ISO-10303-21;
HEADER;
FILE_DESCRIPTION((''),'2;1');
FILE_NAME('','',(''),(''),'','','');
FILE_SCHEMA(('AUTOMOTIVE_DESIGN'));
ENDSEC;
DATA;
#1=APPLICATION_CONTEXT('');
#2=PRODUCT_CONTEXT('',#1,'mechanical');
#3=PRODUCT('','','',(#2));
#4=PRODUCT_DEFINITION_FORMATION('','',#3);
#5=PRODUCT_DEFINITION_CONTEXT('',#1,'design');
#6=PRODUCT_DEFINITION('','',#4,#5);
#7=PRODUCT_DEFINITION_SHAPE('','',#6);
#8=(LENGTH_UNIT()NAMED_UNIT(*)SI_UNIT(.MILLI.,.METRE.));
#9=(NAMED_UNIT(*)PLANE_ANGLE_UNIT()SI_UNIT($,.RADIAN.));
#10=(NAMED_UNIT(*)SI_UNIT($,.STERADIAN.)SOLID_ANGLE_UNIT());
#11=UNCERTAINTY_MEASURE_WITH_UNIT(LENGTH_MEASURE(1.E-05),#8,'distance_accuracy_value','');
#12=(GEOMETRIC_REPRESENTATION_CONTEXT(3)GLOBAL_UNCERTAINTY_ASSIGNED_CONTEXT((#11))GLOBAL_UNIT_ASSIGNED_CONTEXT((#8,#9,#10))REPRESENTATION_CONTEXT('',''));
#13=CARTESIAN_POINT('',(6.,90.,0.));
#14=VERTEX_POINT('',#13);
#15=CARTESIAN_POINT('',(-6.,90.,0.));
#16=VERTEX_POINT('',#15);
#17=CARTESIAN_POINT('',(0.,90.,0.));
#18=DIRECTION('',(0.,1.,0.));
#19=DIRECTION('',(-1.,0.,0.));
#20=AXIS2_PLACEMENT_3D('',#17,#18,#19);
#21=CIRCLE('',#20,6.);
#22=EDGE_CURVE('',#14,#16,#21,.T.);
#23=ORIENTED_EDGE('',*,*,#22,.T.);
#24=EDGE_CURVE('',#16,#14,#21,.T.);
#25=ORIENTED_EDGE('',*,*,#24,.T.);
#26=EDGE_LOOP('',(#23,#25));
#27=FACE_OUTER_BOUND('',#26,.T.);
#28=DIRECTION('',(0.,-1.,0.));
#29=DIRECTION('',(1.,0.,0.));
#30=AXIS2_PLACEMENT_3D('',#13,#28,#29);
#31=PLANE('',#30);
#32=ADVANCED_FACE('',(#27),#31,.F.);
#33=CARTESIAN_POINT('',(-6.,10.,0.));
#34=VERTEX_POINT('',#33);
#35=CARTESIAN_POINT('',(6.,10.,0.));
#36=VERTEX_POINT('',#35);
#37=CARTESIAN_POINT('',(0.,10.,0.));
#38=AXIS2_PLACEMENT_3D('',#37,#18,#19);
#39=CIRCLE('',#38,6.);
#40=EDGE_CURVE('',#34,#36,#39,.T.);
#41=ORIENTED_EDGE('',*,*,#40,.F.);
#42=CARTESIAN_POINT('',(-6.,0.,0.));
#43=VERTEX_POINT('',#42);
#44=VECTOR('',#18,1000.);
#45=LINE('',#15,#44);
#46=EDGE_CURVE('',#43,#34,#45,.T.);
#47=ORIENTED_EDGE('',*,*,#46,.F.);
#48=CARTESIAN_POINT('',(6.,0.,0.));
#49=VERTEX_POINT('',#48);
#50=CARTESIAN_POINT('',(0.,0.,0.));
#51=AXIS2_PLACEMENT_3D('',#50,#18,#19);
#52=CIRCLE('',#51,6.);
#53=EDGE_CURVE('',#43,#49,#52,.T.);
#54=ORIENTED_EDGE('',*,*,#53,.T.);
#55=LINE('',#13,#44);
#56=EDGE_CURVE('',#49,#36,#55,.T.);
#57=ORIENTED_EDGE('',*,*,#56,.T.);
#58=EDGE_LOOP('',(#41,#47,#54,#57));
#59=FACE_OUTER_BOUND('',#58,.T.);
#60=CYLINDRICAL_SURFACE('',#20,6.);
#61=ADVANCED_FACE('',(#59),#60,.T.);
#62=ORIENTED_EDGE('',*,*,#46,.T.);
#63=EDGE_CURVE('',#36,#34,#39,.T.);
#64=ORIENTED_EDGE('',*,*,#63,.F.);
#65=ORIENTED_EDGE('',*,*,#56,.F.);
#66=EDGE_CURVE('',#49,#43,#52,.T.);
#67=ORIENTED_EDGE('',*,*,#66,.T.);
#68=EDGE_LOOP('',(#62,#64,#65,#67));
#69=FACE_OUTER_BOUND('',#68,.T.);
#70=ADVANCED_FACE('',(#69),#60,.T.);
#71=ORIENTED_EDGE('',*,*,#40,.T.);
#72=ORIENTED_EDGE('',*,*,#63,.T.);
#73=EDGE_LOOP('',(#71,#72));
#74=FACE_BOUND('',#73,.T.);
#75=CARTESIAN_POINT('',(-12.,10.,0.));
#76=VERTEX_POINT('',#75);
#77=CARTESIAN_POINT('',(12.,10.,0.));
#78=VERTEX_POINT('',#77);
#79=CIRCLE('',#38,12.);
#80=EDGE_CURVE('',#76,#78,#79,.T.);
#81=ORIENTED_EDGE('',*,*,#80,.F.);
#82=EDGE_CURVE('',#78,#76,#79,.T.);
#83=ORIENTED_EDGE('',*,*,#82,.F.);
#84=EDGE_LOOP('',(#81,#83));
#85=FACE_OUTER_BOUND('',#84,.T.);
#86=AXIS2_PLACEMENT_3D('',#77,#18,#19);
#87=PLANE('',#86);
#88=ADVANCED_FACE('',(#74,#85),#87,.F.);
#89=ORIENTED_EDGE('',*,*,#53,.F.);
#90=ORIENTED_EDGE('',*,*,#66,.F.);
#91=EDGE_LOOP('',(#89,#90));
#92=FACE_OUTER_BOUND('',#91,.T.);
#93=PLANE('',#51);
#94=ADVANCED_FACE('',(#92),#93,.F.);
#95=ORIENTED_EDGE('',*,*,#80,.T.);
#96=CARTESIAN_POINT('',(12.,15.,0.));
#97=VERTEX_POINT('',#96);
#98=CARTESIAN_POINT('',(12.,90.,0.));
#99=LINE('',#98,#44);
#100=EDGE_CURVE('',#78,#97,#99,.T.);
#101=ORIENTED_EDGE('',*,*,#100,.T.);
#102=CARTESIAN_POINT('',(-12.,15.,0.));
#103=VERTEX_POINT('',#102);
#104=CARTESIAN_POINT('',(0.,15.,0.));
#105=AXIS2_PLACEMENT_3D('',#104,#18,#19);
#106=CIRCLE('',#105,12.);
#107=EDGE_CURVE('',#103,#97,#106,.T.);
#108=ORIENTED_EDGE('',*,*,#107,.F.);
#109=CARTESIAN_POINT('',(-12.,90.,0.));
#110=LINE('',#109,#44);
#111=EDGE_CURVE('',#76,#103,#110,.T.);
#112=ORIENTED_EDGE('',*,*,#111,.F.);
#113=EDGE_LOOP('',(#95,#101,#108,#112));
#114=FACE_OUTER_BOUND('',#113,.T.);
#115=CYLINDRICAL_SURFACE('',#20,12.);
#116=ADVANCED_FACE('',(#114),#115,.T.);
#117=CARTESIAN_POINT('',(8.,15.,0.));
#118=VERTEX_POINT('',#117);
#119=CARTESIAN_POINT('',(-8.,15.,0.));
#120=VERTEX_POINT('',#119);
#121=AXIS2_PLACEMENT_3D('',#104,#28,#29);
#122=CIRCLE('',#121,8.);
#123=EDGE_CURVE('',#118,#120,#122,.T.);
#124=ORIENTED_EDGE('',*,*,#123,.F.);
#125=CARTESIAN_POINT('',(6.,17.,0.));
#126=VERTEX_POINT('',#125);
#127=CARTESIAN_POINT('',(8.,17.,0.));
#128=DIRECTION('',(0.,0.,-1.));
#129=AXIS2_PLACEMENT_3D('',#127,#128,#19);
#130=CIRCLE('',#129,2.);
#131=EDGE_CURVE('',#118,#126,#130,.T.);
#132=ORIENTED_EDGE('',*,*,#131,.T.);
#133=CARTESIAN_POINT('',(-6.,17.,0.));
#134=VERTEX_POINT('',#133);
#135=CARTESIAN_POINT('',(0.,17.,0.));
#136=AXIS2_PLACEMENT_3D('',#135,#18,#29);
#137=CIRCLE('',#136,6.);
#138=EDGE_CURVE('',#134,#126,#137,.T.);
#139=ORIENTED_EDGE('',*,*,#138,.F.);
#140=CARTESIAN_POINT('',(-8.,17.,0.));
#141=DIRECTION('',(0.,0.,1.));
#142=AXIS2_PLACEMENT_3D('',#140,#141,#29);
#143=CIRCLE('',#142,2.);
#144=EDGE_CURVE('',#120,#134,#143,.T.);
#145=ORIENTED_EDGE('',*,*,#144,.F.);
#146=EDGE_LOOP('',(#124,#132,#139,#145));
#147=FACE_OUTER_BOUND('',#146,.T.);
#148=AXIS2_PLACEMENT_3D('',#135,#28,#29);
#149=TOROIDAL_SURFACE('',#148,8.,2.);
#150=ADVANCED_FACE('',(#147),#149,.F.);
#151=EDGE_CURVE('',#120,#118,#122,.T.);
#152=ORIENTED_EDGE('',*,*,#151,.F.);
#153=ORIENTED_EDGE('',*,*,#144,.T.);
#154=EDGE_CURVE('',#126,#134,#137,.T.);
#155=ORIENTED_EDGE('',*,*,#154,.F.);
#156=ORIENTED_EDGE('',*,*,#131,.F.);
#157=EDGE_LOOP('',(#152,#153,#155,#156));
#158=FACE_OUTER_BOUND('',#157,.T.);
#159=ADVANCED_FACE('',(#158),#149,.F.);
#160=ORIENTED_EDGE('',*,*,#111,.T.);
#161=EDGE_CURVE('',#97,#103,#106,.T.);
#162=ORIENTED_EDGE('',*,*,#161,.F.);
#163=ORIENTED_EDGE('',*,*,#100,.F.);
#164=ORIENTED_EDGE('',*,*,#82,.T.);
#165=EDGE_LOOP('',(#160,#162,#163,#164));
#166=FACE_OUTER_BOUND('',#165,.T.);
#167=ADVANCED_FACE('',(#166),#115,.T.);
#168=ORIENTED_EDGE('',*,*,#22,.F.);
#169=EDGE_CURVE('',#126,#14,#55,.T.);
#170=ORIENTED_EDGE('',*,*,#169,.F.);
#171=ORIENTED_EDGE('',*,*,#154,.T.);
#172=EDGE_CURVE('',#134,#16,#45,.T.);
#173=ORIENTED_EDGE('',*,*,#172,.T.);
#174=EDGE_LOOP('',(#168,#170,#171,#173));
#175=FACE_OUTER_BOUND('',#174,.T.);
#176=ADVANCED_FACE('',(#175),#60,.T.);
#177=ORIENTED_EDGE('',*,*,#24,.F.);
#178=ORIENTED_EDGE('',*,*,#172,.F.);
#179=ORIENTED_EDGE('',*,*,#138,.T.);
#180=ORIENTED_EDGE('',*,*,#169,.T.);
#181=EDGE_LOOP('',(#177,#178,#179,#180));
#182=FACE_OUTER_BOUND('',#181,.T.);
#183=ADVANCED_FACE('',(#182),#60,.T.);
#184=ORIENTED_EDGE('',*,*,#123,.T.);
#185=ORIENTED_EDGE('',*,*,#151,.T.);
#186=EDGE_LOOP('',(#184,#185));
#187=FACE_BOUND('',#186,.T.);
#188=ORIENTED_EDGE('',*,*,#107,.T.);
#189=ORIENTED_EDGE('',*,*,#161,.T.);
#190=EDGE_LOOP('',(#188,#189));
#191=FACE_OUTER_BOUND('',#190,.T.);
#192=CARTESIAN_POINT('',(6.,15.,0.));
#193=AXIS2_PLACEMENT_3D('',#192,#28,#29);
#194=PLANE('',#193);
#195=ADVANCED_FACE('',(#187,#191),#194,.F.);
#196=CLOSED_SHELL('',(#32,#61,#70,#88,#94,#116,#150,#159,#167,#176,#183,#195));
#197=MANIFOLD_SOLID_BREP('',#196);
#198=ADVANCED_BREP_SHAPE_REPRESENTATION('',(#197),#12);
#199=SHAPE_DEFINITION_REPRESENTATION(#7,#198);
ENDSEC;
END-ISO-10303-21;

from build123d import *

# Parameters (mm, degrees)
COLLAR_FILLET_R2_R = 2


with BuildPart() as part:
    # Stand Pin Profile → Stand Pin Body (revolve)
    with BuildSketch(Plane.XY, mode=Mode.PRIVATE) as stand_pin_body_sk:
        Polygon((0, 0), (6, 0), (6, 10), (12, 10), (12, 15), (6, 15), (6, 90), (0, 90), align=None)
    revolve(stand_pin_body_sk.sketch.rotate(Axis((0, 90, 0), (0, -1, 0)), 180), axis=Axis((0, 90, 0), (0, -1, 0)))

    # Collar Fillet R2
    collar_fillet_r2_edges = [part.edges().sort_by_distance(p)[0] for p in [
        (6, 15, 0),
    ]]
    fillet(collar_fillet_r2_edges, radius=COLLAR_FILLET_R2_R)


solid = part.part
